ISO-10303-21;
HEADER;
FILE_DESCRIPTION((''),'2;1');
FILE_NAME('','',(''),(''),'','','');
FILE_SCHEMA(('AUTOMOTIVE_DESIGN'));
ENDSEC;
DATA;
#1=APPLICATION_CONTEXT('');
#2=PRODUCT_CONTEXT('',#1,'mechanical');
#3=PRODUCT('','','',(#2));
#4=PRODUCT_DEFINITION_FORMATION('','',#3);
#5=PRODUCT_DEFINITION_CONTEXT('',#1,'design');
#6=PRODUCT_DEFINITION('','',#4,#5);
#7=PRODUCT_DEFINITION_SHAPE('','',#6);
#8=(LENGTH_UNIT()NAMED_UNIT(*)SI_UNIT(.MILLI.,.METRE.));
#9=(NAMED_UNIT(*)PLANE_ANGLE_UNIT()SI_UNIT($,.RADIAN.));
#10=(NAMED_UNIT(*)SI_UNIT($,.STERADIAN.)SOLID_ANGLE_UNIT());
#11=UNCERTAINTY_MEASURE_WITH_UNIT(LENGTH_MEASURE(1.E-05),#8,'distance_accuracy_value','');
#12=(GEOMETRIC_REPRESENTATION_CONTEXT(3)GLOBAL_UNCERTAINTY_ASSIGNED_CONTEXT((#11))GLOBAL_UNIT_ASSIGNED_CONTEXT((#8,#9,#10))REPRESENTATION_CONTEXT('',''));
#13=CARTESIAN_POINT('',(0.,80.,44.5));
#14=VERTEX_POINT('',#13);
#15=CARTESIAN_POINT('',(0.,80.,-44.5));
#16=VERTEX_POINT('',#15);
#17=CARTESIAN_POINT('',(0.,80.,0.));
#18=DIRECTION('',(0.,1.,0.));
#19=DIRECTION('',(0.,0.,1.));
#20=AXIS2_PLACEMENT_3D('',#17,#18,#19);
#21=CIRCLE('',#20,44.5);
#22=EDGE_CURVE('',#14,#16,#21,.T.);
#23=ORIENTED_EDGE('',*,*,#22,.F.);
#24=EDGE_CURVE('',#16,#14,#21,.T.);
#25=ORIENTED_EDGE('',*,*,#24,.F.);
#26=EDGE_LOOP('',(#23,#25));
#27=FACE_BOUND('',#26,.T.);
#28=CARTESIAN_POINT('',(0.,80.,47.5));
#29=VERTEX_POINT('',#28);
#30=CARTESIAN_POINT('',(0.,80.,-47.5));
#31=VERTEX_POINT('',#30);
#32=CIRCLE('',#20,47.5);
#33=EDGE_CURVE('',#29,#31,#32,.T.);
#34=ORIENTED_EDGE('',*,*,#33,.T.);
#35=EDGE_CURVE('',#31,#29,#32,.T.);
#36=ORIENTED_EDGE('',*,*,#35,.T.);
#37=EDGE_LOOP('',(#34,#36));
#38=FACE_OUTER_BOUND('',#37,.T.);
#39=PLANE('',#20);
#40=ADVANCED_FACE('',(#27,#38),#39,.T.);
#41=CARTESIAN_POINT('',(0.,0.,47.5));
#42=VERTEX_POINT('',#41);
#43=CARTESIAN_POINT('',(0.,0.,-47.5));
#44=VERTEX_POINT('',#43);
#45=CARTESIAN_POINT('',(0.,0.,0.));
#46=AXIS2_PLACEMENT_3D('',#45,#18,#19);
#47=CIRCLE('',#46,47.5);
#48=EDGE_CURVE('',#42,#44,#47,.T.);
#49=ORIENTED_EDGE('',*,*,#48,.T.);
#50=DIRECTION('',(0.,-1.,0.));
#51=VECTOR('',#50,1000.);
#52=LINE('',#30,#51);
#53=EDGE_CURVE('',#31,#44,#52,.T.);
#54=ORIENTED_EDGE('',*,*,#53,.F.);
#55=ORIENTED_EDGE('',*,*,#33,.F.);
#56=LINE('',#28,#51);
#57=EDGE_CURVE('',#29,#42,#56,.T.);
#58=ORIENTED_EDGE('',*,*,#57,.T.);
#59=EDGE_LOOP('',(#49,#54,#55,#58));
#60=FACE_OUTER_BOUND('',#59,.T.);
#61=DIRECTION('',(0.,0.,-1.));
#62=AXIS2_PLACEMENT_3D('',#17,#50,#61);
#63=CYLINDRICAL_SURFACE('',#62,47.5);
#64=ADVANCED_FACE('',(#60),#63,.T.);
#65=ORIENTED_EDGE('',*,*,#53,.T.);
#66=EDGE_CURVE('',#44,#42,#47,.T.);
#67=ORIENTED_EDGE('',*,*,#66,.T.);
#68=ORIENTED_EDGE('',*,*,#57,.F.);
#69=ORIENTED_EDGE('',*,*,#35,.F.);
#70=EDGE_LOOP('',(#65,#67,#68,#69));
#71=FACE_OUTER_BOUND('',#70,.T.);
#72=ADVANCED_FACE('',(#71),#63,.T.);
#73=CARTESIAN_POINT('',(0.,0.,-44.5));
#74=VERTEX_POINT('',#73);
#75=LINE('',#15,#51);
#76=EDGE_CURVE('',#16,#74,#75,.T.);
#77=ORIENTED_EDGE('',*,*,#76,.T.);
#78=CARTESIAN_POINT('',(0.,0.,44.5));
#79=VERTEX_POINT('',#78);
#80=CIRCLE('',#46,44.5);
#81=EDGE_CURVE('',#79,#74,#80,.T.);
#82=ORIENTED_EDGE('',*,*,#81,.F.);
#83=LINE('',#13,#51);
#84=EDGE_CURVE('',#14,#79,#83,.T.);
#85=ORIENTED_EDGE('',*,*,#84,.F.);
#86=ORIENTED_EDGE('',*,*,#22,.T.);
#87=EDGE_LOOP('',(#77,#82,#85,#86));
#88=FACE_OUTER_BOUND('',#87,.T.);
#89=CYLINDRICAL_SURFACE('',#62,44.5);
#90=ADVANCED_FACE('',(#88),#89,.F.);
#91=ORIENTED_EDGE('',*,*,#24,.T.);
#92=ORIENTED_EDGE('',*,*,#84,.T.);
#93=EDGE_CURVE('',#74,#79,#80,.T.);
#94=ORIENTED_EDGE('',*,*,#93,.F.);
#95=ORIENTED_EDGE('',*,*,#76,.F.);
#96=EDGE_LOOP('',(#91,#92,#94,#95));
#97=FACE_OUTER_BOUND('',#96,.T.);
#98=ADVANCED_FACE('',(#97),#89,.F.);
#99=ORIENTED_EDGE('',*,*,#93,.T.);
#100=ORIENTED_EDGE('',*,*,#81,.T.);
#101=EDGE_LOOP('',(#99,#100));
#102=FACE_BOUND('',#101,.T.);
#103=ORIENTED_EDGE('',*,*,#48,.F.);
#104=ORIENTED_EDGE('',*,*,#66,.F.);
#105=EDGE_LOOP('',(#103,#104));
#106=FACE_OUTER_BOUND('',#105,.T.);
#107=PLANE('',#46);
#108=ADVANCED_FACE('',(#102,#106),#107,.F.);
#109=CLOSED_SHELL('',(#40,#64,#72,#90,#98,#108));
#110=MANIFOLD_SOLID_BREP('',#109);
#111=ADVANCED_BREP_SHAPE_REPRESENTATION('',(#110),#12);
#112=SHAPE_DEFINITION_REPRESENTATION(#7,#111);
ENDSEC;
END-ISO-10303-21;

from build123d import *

# Parameters (mm, degrees)
SKETCH_1_R      = 47.5
SKETCH_1_R_2    = 44.5
EXTRUDE_1_DEPTH = 80


with BuildPart() as part:
    # 草图1 → 凸台-拉伸1 (new body)
    with BuildSketch(Plane(origin=(0, 0, 0), x_dir=(1, 0, 0), z_dir=(0, 1, 0))):
        with Locations(Location((0, 0, 0), (0, 0, 270))):
            Circle(SKETCH_1_R)
        with Locations(Location((0, 0, 0), (0, 0, 270))):
            Circle(SKETCH_1_R_2, mode=Mode.SUBTRACT)
    extrude(amount=EXTRUDE_1_DEPTH)


solid = part.part
